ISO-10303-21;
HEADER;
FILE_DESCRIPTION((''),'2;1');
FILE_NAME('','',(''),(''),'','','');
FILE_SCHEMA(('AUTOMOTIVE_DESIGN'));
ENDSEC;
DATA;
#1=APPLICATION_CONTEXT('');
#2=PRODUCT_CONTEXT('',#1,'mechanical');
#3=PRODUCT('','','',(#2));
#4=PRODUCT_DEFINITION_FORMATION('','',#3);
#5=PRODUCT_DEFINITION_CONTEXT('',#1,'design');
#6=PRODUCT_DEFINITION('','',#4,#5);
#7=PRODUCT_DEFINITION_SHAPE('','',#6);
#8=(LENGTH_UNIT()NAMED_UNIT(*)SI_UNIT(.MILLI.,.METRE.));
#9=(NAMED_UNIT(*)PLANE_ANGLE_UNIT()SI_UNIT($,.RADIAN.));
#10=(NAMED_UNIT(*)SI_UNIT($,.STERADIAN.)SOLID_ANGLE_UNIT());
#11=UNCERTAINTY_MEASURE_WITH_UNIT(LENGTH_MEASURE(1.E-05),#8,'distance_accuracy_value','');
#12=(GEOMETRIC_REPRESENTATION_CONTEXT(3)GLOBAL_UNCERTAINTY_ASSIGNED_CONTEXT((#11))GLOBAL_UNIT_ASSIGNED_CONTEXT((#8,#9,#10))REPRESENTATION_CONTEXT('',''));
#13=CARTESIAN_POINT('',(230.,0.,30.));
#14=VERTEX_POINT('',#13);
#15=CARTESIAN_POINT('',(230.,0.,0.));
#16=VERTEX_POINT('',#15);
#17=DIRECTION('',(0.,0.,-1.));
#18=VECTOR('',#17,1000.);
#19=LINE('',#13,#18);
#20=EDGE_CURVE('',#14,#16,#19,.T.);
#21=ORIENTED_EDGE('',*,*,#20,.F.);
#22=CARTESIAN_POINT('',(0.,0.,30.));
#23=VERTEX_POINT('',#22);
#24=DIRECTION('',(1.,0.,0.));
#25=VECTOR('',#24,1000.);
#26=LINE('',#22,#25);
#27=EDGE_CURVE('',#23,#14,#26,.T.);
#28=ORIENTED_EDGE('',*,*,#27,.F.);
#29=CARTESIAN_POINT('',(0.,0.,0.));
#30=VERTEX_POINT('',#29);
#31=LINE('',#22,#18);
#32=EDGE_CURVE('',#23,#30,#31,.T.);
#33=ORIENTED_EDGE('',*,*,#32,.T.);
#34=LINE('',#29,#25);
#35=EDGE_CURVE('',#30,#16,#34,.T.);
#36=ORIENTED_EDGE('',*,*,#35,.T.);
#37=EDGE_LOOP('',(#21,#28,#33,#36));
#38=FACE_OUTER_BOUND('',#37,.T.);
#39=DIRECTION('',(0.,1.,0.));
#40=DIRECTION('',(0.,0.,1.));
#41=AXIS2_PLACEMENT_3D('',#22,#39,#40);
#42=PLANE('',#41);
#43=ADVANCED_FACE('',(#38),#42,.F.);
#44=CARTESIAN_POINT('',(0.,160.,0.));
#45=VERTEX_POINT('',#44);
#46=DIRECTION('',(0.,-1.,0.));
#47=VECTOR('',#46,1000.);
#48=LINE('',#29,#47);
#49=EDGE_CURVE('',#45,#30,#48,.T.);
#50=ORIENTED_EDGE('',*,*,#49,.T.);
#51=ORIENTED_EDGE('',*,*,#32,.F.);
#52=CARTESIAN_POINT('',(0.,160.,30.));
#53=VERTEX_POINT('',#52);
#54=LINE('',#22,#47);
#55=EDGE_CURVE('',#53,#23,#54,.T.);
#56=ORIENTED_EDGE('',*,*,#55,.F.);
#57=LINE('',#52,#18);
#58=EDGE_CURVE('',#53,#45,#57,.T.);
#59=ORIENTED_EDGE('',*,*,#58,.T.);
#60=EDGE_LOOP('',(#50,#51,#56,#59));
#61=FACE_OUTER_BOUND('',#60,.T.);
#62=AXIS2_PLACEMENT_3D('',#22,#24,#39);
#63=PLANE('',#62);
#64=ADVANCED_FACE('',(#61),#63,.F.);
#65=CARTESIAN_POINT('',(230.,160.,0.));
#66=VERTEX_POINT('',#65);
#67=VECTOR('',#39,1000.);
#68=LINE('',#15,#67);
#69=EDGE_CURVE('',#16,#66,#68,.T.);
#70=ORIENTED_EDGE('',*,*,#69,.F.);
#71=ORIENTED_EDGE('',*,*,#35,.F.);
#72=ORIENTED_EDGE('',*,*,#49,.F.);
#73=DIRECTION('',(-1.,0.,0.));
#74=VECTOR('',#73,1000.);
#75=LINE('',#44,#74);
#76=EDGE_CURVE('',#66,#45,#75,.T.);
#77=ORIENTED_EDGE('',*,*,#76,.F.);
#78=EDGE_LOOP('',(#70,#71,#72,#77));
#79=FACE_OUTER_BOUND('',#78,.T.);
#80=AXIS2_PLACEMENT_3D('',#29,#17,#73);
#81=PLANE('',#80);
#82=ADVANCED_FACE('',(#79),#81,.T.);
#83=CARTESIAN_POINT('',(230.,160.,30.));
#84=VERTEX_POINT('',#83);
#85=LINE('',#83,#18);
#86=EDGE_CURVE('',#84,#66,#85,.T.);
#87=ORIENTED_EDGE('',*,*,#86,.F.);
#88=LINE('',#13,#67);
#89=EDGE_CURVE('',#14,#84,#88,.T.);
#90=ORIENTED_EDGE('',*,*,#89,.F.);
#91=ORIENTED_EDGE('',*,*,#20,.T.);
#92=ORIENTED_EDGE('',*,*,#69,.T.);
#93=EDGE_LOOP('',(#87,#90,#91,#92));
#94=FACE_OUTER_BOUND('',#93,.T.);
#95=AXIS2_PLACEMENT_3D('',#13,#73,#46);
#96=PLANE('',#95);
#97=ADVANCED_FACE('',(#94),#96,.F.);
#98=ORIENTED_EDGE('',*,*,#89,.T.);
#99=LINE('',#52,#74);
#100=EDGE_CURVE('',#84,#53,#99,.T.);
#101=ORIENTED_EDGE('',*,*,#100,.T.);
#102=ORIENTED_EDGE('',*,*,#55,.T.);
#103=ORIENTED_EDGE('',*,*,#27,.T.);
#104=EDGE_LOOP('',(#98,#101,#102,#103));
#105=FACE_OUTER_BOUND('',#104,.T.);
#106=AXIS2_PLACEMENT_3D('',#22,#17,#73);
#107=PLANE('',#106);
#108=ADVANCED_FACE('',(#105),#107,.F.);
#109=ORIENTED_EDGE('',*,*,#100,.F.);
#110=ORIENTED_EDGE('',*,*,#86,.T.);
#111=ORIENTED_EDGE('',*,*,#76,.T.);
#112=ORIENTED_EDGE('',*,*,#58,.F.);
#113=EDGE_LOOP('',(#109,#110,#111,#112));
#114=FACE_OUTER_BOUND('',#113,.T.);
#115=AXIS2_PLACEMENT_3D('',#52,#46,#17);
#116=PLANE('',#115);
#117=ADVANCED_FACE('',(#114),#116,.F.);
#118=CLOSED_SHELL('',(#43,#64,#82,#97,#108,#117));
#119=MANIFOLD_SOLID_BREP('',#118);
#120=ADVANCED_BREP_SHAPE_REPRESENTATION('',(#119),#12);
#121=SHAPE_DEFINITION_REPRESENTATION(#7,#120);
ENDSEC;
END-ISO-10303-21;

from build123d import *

# Parameters (mm, degrees)
SKETCH1_W           = 230
SKETCH1_H           = 160
BOSS_EXTRUDE1_DEPTH = 30


with BuildPart() as part:
    # Sketch1 → Boss-Extrude1 (new body)
    with BuildSketch(Plane.XY):
        with Locations((115, 80)):
            Rectangle(SKETCH1_W, SKETCH1_H)
    extrude(amount=BOSS_EXTRUDE1_DEPTH)


solid = part.part
